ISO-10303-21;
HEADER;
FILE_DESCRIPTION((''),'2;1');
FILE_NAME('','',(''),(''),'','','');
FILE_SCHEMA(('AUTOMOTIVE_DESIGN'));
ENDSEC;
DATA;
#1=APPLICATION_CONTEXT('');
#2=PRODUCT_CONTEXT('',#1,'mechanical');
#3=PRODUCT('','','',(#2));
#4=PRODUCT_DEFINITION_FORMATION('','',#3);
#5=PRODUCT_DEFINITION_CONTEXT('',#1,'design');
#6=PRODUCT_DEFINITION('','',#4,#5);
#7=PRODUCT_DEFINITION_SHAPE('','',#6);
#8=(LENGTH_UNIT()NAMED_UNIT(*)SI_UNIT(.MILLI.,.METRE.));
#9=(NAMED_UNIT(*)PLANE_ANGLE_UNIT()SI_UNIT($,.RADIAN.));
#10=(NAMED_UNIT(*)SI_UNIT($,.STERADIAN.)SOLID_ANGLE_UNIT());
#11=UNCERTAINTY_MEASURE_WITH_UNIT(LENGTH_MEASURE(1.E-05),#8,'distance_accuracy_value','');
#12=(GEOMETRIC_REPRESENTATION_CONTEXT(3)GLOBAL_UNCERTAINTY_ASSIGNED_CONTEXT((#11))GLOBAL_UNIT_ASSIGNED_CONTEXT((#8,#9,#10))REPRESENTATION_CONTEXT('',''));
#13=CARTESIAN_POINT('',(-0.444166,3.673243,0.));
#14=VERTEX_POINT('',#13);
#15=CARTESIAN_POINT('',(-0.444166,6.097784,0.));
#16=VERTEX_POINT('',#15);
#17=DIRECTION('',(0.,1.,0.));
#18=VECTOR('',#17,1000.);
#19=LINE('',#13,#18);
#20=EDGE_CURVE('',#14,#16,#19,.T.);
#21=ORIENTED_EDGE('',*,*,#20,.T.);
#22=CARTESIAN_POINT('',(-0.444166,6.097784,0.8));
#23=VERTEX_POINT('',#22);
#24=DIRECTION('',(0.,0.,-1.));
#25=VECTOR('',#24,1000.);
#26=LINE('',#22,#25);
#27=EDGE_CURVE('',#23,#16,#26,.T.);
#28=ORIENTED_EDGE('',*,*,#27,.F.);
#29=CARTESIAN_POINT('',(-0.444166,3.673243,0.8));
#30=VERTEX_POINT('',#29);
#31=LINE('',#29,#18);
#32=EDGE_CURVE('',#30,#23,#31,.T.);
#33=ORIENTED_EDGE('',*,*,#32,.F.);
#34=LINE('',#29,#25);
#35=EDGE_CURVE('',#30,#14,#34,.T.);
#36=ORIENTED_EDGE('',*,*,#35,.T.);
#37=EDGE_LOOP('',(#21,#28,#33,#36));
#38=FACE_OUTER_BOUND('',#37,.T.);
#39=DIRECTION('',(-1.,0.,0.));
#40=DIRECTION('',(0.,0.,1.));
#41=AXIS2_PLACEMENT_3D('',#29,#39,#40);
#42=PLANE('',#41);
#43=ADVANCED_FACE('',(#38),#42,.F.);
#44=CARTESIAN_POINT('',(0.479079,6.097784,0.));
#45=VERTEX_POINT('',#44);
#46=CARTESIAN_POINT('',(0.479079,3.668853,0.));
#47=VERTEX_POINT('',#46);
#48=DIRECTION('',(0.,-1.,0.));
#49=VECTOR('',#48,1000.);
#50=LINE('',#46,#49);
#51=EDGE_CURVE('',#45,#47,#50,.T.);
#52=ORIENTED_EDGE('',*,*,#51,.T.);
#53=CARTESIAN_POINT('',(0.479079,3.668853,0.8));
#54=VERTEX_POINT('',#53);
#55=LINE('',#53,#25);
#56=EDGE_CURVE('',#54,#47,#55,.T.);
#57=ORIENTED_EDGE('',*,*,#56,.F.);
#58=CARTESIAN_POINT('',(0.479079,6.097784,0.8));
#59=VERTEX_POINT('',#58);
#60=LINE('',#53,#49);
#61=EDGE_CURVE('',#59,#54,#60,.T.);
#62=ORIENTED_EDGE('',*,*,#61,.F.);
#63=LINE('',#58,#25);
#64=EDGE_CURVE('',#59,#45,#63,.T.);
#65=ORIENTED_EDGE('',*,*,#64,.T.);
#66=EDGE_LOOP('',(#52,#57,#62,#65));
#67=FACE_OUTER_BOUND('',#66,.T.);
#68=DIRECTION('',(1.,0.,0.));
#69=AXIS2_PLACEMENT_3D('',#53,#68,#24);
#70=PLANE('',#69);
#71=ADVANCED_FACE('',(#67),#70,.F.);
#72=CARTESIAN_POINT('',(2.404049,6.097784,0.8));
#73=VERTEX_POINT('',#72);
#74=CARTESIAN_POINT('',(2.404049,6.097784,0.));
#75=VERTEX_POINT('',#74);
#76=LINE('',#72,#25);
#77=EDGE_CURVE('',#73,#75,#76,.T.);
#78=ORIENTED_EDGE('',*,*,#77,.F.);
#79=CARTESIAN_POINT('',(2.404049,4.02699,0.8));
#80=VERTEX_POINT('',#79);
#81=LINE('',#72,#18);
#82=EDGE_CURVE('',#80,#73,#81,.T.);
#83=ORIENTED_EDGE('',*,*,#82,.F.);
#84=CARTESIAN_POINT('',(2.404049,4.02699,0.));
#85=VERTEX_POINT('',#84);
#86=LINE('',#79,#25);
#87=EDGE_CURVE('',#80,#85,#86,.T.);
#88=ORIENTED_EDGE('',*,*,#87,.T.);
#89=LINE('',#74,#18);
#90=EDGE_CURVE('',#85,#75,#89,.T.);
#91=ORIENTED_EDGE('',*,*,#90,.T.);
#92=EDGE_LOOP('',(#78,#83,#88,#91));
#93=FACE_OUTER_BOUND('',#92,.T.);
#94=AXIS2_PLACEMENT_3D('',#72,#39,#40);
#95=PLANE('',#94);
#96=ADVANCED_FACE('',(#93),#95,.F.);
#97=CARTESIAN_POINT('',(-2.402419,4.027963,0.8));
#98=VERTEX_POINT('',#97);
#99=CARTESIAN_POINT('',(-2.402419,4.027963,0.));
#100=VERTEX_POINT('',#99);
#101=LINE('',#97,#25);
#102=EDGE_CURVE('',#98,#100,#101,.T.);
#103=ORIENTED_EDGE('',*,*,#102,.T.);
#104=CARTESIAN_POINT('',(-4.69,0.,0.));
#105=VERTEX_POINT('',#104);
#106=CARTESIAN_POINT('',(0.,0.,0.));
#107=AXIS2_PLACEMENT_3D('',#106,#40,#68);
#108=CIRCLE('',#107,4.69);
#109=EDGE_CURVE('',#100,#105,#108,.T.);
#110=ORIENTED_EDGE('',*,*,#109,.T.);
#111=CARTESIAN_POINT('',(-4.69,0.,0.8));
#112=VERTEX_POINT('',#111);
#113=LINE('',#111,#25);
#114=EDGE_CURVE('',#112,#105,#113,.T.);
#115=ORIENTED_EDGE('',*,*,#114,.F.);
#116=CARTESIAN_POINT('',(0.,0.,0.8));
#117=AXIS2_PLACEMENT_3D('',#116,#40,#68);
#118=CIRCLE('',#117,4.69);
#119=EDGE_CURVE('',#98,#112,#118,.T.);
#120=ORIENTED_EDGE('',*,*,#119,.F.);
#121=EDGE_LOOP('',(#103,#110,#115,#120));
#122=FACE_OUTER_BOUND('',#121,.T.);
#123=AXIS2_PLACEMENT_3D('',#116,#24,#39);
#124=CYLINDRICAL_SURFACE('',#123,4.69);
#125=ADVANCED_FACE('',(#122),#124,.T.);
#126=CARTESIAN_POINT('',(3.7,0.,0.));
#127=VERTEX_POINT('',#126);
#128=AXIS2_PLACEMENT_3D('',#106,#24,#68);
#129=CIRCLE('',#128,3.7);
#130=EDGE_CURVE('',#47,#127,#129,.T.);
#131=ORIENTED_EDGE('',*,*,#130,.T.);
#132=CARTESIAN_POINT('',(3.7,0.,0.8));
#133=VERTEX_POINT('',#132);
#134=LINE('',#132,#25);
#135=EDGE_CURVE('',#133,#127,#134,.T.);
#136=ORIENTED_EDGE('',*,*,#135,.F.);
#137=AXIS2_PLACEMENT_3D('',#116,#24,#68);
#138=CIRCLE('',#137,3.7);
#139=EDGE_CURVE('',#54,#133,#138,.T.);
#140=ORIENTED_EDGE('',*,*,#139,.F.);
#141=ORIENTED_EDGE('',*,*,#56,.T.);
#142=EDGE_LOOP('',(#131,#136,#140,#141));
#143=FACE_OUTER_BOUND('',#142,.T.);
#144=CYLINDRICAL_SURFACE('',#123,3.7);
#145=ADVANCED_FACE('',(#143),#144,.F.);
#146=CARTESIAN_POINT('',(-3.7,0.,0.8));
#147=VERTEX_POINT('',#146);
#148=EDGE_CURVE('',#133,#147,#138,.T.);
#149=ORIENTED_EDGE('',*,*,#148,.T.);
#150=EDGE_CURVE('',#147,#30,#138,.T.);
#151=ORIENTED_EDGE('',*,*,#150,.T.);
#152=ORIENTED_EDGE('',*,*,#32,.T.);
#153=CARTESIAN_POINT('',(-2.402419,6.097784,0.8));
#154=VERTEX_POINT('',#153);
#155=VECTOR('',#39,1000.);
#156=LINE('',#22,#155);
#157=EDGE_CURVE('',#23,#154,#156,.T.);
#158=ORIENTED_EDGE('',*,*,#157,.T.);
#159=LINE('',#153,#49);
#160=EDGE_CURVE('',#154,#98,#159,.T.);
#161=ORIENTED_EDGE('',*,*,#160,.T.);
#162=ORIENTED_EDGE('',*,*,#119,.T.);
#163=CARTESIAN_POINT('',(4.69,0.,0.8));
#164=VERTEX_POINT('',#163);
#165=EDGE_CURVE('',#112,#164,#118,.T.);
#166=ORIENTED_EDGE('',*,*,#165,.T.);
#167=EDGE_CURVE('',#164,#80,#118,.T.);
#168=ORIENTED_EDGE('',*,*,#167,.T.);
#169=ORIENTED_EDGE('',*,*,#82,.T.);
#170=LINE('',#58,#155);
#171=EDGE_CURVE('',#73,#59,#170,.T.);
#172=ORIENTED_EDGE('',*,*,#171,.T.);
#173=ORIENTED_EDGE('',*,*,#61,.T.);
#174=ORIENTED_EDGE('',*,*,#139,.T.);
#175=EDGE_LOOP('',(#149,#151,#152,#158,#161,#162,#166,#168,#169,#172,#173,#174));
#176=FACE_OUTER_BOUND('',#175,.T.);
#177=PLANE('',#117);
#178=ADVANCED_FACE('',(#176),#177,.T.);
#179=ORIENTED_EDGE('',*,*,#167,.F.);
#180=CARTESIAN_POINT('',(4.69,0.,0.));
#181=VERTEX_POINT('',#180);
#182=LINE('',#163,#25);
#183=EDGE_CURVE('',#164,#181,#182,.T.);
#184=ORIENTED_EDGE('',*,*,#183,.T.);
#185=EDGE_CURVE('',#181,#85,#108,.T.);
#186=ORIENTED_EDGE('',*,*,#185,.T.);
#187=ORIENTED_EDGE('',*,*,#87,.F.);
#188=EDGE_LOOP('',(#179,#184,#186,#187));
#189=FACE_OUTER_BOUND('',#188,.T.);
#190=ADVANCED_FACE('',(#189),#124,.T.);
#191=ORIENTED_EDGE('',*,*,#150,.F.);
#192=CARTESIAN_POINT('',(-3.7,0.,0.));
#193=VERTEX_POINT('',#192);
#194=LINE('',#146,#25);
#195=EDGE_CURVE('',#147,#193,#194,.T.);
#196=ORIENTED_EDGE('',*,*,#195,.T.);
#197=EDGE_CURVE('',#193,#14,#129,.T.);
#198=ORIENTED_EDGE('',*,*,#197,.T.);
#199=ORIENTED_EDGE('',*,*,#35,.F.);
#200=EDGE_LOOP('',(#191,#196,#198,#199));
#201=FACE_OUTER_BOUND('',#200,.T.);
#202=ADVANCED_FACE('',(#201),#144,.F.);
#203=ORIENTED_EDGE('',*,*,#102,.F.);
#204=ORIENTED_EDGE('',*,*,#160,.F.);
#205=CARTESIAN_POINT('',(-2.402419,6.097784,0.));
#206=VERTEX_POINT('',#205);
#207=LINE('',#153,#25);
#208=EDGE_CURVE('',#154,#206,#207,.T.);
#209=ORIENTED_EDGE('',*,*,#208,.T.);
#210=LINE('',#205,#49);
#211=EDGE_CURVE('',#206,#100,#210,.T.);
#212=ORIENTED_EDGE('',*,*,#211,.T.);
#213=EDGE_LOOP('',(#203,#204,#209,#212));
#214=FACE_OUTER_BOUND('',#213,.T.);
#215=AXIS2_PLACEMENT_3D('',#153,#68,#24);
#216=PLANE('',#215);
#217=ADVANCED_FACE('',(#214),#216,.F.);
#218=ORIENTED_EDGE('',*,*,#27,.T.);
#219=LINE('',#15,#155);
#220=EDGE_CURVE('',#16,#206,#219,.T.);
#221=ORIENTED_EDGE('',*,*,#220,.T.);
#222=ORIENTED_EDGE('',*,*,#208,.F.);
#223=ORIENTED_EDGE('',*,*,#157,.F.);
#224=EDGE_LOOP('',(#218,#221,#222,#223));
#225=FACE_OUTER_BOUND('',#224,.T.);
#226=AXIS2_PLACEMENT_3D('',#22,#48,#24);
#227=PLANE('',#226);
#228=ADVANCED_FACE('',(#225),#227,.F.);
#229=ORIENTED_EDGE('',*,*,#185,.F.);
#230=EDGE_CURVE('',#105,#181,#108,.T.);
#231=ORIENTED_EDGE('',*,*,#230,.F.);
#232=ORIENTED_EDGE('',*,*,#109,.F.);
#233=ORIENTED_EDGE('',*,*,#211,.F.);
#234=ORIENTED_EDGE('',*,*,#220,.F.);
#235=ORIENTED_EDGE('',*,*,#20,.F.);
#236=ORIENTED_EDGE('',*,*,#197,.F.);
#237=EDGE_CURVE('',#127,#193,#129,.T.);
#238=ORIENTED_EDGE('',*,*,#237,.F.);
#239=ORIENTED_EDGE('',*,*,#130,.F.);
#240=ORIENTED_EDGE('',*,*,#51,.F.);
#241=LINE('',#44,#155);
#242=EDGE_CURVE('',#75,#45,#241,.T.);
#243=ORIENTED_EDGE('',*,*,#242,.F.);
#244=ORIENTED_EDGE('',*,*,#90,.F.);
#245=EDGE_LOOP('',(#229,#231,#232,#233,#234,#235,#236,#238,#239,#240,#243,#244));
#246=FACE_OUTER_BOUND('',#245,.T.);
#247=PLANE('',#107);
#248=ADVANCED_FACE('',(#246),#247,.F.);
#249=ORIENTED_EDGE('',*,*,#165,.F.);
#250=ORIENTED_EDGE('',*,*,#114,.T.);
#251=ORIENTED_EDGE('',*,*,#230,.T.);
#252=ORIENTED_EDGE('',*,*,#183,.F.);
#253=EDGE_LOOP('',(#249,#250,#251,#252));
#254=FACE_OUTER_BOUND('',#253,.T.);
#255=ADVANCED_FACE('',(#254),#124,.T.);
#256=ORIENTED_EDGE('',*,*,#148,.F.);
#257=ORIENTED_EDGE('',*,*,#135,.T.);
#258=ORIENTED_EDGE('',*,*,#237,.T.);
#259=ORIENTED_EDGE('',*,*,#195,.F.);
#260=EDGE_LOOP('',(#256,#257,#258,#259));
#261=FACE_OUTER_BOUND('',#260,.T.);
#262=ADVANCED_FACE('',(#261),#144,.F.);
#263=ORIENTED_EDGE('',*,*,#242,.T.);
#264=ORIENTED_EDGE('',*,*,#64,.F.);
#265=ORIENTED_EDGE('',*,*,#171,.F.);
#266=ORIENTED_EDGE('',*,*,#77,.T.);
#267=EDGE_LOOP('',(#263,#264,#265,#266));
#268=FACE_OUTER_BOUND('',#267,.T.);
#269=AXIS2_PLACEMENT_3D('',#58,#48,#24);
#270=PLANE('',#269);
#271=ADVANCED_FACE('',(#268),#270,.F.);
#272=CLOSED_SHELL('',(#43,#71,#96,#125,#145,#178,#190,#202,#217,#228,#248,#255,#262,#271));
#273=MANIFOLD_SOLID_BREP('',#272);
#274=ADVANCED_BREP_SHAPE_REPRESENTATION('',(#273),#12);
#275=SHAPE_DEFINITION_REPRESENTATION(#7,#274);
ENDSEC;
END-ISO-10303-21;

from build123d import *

# Parameters (mm, degrees)
BOSS_EXTRUDE1_DEPTH = 0.8


with BuildPart() as part:
    # Sketch1 → Boss-Extrude1 (new body)
    with BuildSketch(Plane.XY):
        with BuildLine():
            Line((-0.44416607, 3.673243322), (-0.44416607, 6.097784133))
            Line((-0.44416607, 6.097784133), (-2.402419126, 6.097784133))
            Line((-2.402419126, 6.097784133), (-2.402419126, 4.027962555))
            ThreePointArc((-2.402419126, 4.027962555), (-0.000948808, -4.689999904), (2.404048678, 4.026990186))
            Line((2.404048678, 4.026990186), (2.404048678, 6.097784133))
            Line((2.404048678, 6.097784133), (0.479079413, 6.097784133))
            Line((0.479079413, 6.097784133), (0.479079413, 3.668853079))
            ThreePointArc((0.479079413, 3.668853079), (-0.017594145, -3.699958168), (-0.44416607, 3.673243322))
        make_face()
    extrude(amount=BOSS_EXTRUDE1_DEPTH)


solid = part.part
